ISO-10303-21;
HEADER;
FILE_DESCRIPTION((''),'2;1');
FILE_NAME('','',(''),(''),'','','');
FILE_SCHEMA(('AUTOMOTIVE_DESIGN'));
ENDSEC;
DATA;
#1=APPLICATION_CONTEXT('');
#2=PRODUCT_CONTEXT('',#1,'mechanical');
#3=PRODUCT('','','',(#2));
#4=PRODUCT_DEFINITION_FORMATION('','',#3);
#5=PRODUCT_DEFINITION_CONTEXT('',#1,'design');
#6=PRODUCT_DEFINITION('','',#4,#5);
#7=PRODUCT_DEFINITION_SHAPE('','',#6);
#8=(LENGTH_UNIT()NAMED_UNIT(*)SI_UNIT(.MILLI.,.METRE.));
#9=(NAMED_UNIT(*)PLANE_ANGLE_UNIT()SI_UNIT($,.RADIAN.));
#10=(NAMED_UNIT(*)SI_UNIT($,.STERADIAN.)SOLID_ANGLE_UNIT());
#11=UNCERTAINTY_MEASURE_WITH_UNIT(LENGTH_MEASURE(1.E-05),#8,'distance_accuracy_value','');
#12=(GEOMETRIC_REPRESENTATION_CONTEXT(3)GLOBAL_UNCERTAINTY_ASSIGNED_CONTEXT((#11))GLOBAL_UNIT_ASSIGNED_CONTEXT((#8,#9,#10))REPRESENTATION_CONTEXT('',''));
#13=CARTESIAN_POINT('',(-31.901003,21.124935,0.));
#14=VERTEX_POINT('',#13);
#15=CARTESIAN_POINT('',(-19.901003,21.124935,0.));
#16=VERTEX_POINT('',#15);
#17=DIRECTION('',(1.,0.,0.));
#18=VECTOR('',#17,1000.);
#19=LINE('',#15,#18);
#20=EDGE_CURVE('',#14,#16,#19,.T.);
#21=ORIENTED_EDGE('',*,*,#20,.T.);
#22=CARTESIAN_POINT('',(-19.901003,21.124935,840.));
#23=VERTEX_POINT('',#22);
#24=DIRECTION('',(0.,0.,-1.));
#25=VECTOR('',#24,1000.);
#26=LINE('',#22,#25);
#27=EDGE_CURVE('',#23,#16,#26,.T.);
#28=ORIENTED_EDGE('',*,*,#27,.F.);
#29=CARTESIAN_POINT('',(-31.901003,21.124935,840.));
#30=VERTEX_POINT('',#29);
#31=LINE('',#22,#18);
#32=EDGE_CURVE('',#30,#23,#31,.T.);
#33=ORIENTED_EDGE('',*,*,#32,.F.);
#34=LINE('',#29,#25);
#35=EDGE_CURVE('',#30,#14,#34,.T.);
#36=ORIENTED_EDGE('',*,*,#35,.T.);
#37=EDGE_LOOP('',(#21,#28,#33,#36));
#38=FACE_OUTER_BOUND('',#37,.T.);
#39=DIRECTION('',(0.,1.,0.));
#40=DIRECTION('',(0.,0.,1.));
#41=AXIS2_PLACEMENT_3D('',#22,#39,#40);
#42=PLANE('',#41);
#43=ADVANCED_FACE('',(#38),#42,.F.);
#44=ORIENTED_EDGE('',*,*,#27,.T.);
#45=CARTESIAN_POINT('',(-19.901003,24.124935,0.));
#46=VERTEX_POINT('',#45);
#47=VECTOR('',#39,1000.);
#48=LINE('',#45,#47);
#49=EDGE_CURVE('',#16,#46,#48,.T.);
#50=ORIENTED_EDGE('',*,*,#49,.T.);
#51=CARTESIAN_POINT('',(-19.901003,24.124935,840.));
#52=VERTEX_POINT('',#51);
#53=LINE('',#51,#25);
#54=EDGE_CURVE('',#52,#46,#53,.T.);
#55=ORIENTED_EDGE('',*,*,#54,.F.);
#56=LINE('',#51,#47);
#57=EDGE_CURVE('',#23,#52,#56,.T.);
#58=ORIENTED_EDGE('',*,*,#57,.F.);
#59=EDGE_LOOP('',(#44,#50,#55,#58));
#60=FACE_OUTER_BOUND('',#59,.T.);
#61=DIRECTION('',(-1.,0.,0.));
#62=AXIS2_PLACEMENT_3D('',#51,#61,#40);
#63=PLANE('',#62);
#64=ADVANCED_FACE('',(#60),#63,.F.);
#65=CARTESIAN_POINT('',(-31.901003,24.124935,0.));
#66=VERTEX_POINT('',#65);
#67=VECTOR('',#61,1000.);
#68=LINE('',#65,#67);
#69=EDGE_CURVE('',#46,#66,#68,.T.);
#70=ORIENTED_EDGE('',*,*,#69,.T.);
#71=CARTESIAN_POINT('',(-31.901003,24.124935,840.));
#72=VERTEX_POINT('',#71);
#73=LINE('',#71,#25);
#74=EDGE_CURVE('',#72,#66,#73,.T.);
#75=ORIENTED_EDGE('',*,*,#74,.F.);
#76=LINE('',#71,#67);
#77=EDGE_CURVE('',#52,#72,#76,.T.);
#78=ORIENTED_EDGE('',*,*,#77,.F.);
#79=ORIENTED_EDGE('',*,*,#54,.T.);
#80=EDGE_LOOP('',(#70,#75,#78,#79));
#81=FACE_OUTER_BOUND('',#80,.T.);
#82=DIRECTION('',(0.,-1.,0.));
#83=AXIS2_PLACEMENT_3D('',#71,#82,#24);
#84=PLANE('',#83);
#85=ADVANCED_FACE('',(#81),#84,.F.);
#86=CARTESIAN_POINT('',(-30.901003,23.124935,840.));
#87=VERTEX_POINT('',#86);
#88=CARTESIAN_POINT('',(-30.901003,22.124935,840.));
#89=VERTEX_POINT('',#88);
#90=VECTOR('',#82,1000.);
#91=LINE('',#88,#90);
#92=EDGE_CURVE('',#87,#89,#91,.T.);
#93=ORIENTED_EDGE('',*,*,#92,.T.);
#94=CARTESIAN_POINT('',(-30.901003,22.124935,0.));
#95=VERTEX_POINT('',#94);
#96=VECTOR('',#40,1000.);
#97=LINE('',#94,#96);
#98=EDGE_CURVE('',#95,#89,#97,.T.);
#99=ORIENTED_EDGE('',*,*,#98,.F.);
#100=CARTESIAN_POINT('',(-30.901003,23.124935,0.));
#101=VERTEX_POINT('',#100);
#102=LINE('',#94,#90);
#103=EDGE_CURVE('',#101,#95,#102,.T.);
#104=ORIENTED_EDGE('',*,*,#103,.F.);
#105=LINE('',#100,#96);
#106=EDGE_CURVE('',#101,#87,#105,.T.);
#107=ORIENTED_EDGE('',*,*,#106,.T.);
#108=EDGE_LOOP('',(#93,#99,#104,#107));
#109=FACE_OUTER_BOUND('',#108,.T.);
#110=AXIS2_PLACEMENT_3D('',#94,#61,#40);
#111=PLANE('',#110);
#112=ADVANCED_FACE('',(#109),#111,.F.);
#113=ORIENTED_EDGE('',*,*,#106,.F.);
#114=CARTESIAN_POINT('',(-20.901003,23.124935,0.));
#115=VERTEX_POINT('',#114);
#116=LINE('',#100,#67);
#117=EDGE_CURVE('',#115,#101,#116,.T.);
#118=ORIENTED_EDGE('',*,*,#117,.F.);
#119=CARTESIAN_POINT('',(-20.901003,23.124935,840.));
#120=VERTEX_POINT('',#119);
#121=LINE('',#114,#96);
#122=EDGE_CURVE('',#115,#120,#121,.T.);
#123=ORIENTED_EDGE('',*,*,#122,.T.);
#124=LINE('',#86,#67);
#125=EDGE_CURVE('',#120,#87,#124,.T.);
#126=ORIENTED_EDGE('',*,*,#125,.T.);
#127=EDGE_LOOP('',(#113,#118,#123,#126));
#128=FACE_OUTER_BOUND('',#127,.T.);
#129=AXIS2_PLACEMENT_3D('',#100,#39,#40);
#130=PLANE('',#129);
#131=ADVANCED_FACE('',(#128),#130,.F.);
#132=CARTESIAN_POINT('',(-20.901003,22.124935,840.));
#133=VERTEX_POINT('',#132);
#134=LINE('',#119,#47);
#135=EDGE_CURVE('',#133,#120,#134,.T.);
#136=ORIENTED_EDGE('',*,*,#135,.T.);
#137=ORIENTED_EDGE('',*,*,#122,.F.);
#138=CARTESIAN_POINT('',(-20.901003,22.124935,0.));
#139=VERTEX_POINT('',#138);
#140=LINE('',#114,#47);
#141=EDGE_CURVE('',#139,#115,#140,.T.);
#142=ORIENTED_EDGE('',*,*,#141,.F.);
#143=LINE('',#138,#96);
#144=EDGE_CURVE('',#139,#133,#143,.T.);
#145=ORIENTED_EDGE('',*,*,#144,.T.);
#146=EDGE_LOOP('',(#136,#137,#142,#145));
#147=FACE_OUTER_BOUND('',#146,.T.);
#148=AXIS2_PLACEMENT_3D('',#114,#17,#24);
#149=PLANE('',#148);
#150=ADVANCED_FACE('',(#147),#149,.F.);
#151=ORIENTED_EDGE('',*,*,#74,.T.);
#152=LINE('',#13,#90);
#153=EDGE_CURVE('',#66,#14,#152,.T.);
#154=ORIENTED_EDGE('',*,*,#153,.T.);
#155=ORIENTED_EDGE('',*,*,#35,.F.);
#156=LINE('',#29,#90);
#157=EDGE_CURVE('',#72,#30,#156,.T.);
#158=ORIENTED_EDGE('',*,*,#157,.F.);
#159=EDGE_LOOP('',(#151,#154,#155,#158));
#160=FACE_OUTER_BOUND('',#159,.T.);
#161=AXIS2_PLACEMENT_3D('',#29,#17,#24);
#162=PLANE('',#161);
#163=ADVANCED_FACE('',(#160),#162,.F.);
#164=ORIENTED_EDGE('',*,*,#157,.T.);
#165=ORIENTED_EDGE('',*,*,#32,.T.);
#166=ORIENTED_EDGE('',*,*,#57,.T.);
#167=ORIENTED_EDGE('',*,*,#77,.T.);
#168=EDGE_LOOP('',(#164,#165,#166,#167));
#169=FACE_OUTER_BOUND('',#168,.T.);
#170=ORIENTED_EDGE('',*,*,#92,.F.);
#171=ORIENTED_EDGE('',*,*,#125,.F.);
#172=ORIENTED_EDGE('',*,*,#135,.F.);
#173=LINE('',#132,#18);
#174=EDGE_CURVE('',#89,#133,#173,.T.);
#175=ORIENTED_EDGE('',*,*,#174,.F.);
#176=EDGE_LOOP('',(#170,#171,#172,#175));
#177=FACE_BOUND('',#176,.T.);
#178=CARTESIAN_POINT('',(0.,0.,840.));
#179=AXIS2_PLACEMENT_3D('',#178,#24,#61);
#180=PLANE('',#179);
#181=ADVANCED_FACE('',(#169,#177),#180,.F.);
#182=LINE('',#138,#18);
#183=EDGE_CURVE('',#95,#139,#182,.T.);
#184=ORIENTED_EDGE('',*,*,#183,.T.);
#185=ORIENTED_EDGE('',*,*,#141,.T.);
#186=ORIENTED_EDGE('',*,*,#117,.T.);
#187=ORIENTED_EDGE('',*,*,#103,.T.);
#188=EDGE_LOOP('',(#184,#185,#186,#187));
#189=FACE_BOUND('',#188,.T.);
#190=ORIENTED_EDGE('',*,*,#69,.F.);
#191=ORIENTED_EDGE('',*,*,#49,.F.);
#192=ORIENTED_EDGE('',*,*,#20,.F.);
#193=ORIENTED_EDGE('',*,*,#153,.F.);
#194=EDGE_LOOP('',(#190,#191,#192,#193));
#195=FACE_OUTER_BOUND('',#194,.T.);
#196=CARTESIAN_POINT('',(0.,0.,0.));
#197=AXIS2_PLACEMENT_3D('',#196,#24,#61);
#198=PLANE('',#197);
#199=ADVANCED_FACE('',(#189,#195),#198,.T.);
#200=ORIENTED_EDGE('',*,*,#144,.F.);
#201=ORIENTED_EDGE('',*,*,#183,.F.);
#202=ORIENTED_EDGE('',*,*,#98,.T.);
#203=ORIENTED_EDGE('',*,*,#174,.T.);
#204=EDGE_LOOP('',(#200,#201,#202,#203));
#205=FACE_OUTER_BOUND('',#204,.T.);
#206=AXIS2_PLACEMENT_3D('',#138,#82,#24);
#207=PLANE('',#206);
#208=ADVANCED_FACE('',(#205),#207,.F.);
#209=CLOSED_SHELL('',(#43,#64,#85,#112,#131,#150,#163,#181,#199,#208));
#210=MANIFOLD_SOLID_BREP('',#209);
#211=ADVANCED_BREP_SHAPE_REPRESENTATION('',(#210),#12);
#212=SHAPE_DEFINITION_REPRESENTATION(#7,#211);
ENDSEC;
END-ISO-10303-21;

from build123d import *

# Parameters (mm, degrees)
SKETCH1_W           = 12
SKETCH1_H           = 3
BOSS_EXTRUDE1_DEPTH = 840
SKETCH2_W           = 10
SKETCH2_H           = 1
CUT_EXTRUDE1_DEPTH  = 841.951655259


with BuildPart() as part:
    # Sketch1 → Boss-Extrude1 (new body)
    with BuildSketch(Plane.XY):
        with Locations((-25.901003365, 22.624934563)):
            Rectangle(SKETCH1_W, SKETCH1_H)
    extrude(amount=BOSS_EXTRUDE1_DEPTH)

    # Sketch2 → Cut-Extrude1 (cut, through all)
    with BuildSketch(Plane.XY.offset(840)):
        with Locations((-25.901003365, 22.624934563)):
            Rectangle(SKETCH2_W, SKETCH2_H)
    extrude(amount=-CUT_EXTRUDE1_DEPTH, mode=Mode.SUBTRACT)


solid = part.part
